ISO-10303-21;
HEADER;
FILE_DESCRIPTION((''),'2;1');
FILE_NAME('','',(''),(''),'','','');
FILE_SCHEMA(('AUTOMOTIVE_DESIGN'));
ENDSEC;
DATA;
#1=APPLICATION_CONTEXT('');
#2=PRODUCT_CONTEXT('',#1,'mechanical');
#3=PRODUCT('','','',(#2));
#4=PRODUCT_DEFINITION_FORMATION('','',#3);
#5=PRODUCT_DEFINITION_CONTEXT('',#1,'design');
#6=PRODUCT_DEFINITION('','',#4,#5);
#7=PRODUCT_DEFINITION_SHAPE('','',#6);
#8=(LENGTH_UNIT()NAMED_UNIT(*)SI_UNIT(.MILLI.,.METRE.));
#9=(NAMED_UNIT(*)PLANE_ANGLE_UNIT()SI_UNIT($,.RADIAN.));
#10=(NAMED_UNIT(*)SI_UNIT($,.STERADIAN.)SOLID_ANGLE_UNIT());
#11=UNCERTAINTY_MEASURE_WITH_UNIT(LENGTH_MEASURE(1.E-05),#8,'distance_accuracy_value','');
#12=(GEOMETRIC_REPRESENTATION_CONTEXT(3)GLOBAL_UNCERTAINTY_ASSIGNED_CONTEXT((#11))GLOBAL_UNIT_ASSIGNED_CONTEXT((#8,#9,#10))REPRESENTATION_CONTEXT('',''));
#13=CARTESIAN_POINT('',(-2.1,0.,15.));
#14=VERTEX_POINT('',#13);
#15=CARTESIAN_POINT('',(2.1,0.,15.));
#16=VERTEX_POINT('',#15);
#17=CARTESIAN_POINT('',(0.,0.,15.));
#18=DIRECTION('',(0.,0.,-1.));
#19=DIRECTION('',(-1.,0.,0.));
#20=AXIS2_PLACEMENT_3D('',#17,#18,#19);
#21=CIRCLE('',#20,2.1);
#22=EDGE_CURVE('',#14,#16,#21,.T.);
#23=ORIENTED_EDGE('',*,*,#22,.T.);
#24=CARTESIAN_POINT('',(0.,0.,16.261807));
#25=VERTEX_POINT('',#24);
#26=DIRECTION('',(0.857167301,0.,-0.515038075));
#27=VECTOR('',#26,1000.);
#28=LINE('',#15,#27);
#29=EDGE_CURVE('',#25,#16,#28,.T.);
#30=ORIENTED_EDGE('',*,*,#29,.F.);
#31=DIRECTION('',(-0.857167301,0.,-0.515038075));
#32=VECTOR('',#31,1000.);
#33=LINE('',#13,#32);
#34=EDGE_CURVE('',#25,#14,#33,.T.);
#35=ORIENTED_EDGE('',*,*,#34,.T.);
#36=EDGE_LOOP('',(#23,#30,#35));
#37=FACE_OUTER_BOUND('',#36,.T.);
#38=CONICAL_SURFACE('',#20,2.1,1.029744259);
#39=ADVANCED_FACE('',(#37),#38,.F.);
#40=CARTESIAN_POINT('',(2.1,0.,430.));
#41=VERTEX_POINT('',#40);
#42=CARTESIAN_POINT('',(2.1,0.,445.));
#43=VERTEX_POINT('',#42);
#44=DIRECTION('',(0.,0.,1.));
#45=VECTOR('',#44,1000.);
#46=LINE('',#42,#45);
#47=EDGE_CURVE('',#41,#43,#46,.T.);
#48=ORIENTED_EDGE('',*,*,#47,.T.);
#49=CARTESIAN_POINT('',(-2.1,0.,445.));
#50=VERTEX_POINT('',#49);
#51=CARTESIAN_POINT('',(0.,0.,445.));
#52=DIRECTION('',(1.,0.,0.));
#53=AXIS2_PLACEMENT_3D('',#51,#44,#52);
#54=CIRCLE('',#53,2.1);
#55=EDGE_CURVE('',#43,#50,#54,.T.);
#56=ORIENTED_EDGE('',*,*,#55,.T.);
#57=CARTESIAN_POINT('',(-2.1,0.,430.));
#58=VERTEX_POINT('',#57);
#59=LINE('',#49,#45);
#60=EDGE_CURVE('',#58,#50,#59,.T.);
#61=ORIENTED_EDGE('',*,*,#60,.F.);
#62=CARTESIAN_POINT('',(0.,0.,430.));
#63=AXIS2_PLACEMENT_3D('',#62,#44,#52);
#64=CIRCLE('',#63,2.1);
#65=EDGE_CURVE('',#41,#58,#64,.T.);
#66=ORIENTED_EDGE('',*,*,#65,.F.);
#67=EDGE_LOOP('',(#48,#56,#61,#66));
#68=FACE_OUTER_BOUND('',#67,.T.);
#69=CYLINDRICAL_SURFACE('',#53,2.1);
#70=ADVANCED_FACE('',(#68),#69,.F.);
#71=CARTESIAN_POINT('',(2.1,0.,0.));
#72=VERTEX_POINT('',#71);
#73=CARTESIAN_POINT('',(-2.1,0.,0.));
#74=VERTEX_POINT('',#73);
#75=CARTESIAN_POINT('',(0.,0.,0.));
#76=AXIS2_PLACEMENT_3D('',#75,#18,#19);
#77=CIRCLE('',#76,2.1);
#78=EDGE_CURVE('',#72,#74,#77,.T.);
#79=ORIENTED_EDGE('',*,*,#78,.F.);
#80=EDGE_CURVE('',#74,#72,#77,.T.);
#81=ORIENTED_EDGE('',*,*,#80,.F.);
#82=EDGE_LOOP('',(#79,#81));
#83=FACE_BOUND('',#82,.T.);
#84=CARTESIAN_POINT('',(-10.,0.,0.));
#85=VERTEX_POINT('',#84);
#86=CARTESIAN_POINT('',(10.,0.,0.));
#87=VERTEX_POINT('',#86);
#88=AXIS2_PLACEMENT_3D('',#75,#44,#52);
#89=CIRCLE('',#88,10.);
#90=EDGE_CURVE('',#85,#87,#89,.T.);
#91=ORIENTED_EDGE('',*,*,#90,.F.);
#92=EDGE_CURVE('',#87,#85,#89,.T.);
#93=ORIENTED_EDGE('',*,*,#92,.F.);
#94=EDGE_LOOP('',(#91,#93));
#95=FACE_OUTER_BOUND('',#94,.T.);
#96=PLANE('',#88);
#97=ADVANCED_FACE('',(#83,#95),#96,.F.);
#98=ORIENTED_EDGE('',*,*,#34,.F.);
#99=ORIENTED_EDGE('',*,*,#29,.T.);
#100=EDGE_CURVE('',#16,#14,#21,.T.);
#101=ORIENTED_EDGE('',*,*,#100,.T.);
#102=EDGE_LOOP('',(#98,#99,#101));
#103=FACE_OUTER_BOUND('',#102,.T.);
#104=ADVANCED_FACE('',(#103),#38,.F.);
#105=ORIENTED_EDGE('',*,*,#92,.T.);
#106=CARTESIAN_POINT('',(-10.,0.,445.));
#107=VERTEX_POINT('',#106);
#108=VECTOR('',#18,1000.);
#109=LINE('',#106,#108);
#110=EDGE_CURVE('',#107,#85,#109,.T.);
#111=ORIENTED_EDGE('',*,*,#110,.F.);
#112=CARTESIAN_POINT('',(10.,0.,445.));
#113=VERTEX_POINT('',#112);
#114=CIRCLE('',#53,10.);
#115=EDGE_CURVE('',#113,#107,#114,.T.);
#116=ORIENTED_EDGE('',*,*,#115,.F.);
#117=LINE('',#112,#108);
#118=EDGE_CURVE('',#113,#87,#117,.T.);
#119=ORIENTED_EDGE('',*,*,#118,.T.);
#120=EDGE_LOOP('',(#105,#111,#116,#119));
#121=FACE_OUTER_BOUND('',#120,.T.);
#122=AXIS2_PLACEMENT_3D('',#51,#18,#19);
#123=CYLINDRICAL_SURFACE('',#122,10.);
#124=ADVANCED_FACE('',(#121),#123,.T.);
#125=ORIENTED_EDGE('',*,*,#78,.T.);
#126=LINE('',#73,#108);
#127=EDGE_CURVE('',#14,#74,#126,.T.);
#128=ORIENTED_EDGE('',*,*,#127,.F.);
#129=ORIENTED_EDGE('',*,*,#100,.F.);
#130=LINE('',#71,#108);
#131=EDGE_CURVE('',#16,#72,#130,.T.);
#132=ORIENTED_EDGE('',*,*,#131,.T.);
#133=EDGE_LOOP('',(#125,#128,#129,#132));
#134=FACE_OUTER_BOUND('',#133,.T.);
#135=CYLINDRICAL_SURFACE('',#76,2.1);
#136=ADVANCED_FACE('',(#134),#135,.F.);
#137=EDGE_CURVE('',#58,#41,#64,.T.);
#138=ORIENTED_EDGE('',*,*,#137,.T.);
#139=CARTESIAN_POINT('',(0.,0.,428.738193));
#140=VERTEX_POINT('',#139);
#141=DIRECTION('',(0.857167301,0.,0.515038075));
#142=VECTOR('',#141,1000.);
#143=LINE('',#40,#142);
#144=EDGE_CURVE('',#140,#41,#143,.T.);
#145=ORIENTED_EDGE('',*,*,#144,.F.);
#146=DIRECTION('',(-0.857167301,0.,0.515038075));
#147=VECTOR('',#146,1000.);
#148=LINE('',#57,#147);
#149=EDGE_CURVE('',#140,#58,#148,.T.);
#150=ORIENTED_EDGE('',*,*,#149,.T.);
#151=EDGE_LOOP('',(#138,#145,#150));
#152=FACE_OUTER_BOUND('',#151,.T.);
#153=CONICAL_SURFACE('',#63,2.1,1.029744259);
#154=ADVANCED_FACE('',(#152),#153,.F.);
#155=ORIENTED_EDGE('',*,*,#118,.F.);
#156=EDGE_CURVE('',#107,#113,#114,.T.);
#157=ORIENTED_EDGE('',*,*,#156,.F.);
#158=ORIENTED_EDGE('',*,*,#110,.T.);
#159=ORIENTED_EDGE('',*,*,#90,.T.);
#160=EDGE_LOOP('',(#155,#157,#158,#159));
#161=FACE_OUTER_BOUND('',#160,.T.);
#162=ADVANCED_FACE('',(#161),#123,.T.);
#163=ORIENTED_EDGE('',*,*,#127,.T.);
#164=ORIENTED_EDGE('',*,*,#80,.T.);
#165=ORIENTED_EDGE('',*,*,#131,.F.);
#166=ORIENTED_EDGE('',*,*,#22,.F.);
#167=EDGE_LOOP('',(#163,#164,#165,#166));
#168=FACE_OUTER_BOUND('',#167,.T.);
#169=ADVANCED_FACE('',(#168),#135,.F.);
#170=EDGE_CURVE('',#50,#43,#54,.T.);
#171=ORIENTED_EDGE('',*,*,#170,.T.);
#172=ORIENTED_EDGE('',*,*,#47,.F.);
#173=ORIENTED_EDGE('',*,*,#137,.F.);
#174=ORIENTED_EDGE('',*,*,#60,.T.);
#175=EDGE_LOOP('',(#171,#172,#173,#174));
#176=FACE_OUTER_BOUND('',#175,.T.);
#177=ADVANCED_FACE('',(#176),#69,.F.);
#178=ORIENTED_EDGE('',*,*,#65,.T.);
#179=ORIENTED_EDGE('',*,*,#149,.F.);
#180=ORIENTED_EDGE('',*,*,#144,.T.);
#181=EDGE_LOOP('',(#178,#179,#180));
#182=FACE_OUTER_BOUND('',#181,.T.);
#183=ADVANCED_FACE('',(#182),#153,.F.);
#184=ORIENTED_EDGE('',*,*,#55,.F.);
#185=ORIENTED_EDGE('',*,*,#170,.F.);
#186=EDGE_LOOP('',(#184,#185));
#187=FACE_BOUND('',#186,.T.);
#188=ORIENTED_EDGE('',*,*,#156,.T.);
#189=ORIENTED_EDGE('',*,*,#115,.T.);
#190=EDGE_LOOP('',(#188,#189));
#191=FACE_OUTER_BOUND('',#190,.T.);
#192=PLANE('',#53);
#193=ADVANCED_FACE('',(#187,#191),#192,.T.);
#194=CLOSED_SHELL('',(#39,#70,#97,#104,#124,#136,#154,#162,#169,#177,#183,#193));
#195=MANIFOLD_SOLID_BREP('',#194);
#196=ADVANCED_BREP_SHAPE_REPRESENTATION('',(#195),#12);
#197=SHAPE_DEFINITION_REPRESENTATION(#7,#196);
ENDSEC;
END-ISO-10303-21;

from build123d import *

# Parameters (mm, degrees)
SKETCH_1_R             = 10
EXTRUDE_1_DEPTH        = 445
HOLE_WIZARD_M5_1_D     = 4.2
HOLE_WIZARD_M5_1_DEPTH = 15
HOLE_WIZARD_M5_1_TIP   = 1.2618073
HOLE_WIZARD_M5_2_D     = 4.2
HOLE_WIZARD_M5_2_DEPTH = 15
HOLE_WIZARD_M5_2_TIP   = 1.2618073


with BuildPart() as part:
    # 草图1 → 凸台-拉伸1 (new body)
    with BuildSketch(Plane.XY):
        Circle(SKETCH_1_R)
    extrude(amount=EXTRUDE_1_DEPTH)

    # M5 螺纹孔1
    with Locations(Plane.XY.offset(445)):
        with Locations((0, 0)):
            Hole(HOLE_WIZARD_M5_1_D / 2, depth=HOLE_WIZARD_M5_1_DEPTH)
            with Locations((0, 0, -(HOLE_WIZARD_M5_1_DEPTH + HOLE_WIZARD_M5_1_TIP / 2))):  # 118° drill point
                Cone(0, HOLE_WIZARD_M5_1_D / 2, HOLE_WIZARD_M5_1_TIP, mode=Mode.SUBTRACT)

    # M5 螺纹孔2
    with Locations(Plane(origin=(0, 0, 0), x_dir=(-1, 0, 0), z_dir=(0, 0, -1))):
        with Locations((0, 0)):
            Hole(HOLE_WIZARD_M5_2_D / 2, depth=HOLE_WIZARD_M5_2_DEPTH)
            with Locations((0, 0, -(HOLE_WIZARD_M5_2_DEPTH + HOLE_WIZARD_M5_2_TIP / 2))):  # 118° drill point
                Cone(0, HOLE_WIZARD_M5_2_D / 2, HOLE_WIZARD_M5_2_TIP, mode=Mode.SUBTRACT)


solid = part.part
